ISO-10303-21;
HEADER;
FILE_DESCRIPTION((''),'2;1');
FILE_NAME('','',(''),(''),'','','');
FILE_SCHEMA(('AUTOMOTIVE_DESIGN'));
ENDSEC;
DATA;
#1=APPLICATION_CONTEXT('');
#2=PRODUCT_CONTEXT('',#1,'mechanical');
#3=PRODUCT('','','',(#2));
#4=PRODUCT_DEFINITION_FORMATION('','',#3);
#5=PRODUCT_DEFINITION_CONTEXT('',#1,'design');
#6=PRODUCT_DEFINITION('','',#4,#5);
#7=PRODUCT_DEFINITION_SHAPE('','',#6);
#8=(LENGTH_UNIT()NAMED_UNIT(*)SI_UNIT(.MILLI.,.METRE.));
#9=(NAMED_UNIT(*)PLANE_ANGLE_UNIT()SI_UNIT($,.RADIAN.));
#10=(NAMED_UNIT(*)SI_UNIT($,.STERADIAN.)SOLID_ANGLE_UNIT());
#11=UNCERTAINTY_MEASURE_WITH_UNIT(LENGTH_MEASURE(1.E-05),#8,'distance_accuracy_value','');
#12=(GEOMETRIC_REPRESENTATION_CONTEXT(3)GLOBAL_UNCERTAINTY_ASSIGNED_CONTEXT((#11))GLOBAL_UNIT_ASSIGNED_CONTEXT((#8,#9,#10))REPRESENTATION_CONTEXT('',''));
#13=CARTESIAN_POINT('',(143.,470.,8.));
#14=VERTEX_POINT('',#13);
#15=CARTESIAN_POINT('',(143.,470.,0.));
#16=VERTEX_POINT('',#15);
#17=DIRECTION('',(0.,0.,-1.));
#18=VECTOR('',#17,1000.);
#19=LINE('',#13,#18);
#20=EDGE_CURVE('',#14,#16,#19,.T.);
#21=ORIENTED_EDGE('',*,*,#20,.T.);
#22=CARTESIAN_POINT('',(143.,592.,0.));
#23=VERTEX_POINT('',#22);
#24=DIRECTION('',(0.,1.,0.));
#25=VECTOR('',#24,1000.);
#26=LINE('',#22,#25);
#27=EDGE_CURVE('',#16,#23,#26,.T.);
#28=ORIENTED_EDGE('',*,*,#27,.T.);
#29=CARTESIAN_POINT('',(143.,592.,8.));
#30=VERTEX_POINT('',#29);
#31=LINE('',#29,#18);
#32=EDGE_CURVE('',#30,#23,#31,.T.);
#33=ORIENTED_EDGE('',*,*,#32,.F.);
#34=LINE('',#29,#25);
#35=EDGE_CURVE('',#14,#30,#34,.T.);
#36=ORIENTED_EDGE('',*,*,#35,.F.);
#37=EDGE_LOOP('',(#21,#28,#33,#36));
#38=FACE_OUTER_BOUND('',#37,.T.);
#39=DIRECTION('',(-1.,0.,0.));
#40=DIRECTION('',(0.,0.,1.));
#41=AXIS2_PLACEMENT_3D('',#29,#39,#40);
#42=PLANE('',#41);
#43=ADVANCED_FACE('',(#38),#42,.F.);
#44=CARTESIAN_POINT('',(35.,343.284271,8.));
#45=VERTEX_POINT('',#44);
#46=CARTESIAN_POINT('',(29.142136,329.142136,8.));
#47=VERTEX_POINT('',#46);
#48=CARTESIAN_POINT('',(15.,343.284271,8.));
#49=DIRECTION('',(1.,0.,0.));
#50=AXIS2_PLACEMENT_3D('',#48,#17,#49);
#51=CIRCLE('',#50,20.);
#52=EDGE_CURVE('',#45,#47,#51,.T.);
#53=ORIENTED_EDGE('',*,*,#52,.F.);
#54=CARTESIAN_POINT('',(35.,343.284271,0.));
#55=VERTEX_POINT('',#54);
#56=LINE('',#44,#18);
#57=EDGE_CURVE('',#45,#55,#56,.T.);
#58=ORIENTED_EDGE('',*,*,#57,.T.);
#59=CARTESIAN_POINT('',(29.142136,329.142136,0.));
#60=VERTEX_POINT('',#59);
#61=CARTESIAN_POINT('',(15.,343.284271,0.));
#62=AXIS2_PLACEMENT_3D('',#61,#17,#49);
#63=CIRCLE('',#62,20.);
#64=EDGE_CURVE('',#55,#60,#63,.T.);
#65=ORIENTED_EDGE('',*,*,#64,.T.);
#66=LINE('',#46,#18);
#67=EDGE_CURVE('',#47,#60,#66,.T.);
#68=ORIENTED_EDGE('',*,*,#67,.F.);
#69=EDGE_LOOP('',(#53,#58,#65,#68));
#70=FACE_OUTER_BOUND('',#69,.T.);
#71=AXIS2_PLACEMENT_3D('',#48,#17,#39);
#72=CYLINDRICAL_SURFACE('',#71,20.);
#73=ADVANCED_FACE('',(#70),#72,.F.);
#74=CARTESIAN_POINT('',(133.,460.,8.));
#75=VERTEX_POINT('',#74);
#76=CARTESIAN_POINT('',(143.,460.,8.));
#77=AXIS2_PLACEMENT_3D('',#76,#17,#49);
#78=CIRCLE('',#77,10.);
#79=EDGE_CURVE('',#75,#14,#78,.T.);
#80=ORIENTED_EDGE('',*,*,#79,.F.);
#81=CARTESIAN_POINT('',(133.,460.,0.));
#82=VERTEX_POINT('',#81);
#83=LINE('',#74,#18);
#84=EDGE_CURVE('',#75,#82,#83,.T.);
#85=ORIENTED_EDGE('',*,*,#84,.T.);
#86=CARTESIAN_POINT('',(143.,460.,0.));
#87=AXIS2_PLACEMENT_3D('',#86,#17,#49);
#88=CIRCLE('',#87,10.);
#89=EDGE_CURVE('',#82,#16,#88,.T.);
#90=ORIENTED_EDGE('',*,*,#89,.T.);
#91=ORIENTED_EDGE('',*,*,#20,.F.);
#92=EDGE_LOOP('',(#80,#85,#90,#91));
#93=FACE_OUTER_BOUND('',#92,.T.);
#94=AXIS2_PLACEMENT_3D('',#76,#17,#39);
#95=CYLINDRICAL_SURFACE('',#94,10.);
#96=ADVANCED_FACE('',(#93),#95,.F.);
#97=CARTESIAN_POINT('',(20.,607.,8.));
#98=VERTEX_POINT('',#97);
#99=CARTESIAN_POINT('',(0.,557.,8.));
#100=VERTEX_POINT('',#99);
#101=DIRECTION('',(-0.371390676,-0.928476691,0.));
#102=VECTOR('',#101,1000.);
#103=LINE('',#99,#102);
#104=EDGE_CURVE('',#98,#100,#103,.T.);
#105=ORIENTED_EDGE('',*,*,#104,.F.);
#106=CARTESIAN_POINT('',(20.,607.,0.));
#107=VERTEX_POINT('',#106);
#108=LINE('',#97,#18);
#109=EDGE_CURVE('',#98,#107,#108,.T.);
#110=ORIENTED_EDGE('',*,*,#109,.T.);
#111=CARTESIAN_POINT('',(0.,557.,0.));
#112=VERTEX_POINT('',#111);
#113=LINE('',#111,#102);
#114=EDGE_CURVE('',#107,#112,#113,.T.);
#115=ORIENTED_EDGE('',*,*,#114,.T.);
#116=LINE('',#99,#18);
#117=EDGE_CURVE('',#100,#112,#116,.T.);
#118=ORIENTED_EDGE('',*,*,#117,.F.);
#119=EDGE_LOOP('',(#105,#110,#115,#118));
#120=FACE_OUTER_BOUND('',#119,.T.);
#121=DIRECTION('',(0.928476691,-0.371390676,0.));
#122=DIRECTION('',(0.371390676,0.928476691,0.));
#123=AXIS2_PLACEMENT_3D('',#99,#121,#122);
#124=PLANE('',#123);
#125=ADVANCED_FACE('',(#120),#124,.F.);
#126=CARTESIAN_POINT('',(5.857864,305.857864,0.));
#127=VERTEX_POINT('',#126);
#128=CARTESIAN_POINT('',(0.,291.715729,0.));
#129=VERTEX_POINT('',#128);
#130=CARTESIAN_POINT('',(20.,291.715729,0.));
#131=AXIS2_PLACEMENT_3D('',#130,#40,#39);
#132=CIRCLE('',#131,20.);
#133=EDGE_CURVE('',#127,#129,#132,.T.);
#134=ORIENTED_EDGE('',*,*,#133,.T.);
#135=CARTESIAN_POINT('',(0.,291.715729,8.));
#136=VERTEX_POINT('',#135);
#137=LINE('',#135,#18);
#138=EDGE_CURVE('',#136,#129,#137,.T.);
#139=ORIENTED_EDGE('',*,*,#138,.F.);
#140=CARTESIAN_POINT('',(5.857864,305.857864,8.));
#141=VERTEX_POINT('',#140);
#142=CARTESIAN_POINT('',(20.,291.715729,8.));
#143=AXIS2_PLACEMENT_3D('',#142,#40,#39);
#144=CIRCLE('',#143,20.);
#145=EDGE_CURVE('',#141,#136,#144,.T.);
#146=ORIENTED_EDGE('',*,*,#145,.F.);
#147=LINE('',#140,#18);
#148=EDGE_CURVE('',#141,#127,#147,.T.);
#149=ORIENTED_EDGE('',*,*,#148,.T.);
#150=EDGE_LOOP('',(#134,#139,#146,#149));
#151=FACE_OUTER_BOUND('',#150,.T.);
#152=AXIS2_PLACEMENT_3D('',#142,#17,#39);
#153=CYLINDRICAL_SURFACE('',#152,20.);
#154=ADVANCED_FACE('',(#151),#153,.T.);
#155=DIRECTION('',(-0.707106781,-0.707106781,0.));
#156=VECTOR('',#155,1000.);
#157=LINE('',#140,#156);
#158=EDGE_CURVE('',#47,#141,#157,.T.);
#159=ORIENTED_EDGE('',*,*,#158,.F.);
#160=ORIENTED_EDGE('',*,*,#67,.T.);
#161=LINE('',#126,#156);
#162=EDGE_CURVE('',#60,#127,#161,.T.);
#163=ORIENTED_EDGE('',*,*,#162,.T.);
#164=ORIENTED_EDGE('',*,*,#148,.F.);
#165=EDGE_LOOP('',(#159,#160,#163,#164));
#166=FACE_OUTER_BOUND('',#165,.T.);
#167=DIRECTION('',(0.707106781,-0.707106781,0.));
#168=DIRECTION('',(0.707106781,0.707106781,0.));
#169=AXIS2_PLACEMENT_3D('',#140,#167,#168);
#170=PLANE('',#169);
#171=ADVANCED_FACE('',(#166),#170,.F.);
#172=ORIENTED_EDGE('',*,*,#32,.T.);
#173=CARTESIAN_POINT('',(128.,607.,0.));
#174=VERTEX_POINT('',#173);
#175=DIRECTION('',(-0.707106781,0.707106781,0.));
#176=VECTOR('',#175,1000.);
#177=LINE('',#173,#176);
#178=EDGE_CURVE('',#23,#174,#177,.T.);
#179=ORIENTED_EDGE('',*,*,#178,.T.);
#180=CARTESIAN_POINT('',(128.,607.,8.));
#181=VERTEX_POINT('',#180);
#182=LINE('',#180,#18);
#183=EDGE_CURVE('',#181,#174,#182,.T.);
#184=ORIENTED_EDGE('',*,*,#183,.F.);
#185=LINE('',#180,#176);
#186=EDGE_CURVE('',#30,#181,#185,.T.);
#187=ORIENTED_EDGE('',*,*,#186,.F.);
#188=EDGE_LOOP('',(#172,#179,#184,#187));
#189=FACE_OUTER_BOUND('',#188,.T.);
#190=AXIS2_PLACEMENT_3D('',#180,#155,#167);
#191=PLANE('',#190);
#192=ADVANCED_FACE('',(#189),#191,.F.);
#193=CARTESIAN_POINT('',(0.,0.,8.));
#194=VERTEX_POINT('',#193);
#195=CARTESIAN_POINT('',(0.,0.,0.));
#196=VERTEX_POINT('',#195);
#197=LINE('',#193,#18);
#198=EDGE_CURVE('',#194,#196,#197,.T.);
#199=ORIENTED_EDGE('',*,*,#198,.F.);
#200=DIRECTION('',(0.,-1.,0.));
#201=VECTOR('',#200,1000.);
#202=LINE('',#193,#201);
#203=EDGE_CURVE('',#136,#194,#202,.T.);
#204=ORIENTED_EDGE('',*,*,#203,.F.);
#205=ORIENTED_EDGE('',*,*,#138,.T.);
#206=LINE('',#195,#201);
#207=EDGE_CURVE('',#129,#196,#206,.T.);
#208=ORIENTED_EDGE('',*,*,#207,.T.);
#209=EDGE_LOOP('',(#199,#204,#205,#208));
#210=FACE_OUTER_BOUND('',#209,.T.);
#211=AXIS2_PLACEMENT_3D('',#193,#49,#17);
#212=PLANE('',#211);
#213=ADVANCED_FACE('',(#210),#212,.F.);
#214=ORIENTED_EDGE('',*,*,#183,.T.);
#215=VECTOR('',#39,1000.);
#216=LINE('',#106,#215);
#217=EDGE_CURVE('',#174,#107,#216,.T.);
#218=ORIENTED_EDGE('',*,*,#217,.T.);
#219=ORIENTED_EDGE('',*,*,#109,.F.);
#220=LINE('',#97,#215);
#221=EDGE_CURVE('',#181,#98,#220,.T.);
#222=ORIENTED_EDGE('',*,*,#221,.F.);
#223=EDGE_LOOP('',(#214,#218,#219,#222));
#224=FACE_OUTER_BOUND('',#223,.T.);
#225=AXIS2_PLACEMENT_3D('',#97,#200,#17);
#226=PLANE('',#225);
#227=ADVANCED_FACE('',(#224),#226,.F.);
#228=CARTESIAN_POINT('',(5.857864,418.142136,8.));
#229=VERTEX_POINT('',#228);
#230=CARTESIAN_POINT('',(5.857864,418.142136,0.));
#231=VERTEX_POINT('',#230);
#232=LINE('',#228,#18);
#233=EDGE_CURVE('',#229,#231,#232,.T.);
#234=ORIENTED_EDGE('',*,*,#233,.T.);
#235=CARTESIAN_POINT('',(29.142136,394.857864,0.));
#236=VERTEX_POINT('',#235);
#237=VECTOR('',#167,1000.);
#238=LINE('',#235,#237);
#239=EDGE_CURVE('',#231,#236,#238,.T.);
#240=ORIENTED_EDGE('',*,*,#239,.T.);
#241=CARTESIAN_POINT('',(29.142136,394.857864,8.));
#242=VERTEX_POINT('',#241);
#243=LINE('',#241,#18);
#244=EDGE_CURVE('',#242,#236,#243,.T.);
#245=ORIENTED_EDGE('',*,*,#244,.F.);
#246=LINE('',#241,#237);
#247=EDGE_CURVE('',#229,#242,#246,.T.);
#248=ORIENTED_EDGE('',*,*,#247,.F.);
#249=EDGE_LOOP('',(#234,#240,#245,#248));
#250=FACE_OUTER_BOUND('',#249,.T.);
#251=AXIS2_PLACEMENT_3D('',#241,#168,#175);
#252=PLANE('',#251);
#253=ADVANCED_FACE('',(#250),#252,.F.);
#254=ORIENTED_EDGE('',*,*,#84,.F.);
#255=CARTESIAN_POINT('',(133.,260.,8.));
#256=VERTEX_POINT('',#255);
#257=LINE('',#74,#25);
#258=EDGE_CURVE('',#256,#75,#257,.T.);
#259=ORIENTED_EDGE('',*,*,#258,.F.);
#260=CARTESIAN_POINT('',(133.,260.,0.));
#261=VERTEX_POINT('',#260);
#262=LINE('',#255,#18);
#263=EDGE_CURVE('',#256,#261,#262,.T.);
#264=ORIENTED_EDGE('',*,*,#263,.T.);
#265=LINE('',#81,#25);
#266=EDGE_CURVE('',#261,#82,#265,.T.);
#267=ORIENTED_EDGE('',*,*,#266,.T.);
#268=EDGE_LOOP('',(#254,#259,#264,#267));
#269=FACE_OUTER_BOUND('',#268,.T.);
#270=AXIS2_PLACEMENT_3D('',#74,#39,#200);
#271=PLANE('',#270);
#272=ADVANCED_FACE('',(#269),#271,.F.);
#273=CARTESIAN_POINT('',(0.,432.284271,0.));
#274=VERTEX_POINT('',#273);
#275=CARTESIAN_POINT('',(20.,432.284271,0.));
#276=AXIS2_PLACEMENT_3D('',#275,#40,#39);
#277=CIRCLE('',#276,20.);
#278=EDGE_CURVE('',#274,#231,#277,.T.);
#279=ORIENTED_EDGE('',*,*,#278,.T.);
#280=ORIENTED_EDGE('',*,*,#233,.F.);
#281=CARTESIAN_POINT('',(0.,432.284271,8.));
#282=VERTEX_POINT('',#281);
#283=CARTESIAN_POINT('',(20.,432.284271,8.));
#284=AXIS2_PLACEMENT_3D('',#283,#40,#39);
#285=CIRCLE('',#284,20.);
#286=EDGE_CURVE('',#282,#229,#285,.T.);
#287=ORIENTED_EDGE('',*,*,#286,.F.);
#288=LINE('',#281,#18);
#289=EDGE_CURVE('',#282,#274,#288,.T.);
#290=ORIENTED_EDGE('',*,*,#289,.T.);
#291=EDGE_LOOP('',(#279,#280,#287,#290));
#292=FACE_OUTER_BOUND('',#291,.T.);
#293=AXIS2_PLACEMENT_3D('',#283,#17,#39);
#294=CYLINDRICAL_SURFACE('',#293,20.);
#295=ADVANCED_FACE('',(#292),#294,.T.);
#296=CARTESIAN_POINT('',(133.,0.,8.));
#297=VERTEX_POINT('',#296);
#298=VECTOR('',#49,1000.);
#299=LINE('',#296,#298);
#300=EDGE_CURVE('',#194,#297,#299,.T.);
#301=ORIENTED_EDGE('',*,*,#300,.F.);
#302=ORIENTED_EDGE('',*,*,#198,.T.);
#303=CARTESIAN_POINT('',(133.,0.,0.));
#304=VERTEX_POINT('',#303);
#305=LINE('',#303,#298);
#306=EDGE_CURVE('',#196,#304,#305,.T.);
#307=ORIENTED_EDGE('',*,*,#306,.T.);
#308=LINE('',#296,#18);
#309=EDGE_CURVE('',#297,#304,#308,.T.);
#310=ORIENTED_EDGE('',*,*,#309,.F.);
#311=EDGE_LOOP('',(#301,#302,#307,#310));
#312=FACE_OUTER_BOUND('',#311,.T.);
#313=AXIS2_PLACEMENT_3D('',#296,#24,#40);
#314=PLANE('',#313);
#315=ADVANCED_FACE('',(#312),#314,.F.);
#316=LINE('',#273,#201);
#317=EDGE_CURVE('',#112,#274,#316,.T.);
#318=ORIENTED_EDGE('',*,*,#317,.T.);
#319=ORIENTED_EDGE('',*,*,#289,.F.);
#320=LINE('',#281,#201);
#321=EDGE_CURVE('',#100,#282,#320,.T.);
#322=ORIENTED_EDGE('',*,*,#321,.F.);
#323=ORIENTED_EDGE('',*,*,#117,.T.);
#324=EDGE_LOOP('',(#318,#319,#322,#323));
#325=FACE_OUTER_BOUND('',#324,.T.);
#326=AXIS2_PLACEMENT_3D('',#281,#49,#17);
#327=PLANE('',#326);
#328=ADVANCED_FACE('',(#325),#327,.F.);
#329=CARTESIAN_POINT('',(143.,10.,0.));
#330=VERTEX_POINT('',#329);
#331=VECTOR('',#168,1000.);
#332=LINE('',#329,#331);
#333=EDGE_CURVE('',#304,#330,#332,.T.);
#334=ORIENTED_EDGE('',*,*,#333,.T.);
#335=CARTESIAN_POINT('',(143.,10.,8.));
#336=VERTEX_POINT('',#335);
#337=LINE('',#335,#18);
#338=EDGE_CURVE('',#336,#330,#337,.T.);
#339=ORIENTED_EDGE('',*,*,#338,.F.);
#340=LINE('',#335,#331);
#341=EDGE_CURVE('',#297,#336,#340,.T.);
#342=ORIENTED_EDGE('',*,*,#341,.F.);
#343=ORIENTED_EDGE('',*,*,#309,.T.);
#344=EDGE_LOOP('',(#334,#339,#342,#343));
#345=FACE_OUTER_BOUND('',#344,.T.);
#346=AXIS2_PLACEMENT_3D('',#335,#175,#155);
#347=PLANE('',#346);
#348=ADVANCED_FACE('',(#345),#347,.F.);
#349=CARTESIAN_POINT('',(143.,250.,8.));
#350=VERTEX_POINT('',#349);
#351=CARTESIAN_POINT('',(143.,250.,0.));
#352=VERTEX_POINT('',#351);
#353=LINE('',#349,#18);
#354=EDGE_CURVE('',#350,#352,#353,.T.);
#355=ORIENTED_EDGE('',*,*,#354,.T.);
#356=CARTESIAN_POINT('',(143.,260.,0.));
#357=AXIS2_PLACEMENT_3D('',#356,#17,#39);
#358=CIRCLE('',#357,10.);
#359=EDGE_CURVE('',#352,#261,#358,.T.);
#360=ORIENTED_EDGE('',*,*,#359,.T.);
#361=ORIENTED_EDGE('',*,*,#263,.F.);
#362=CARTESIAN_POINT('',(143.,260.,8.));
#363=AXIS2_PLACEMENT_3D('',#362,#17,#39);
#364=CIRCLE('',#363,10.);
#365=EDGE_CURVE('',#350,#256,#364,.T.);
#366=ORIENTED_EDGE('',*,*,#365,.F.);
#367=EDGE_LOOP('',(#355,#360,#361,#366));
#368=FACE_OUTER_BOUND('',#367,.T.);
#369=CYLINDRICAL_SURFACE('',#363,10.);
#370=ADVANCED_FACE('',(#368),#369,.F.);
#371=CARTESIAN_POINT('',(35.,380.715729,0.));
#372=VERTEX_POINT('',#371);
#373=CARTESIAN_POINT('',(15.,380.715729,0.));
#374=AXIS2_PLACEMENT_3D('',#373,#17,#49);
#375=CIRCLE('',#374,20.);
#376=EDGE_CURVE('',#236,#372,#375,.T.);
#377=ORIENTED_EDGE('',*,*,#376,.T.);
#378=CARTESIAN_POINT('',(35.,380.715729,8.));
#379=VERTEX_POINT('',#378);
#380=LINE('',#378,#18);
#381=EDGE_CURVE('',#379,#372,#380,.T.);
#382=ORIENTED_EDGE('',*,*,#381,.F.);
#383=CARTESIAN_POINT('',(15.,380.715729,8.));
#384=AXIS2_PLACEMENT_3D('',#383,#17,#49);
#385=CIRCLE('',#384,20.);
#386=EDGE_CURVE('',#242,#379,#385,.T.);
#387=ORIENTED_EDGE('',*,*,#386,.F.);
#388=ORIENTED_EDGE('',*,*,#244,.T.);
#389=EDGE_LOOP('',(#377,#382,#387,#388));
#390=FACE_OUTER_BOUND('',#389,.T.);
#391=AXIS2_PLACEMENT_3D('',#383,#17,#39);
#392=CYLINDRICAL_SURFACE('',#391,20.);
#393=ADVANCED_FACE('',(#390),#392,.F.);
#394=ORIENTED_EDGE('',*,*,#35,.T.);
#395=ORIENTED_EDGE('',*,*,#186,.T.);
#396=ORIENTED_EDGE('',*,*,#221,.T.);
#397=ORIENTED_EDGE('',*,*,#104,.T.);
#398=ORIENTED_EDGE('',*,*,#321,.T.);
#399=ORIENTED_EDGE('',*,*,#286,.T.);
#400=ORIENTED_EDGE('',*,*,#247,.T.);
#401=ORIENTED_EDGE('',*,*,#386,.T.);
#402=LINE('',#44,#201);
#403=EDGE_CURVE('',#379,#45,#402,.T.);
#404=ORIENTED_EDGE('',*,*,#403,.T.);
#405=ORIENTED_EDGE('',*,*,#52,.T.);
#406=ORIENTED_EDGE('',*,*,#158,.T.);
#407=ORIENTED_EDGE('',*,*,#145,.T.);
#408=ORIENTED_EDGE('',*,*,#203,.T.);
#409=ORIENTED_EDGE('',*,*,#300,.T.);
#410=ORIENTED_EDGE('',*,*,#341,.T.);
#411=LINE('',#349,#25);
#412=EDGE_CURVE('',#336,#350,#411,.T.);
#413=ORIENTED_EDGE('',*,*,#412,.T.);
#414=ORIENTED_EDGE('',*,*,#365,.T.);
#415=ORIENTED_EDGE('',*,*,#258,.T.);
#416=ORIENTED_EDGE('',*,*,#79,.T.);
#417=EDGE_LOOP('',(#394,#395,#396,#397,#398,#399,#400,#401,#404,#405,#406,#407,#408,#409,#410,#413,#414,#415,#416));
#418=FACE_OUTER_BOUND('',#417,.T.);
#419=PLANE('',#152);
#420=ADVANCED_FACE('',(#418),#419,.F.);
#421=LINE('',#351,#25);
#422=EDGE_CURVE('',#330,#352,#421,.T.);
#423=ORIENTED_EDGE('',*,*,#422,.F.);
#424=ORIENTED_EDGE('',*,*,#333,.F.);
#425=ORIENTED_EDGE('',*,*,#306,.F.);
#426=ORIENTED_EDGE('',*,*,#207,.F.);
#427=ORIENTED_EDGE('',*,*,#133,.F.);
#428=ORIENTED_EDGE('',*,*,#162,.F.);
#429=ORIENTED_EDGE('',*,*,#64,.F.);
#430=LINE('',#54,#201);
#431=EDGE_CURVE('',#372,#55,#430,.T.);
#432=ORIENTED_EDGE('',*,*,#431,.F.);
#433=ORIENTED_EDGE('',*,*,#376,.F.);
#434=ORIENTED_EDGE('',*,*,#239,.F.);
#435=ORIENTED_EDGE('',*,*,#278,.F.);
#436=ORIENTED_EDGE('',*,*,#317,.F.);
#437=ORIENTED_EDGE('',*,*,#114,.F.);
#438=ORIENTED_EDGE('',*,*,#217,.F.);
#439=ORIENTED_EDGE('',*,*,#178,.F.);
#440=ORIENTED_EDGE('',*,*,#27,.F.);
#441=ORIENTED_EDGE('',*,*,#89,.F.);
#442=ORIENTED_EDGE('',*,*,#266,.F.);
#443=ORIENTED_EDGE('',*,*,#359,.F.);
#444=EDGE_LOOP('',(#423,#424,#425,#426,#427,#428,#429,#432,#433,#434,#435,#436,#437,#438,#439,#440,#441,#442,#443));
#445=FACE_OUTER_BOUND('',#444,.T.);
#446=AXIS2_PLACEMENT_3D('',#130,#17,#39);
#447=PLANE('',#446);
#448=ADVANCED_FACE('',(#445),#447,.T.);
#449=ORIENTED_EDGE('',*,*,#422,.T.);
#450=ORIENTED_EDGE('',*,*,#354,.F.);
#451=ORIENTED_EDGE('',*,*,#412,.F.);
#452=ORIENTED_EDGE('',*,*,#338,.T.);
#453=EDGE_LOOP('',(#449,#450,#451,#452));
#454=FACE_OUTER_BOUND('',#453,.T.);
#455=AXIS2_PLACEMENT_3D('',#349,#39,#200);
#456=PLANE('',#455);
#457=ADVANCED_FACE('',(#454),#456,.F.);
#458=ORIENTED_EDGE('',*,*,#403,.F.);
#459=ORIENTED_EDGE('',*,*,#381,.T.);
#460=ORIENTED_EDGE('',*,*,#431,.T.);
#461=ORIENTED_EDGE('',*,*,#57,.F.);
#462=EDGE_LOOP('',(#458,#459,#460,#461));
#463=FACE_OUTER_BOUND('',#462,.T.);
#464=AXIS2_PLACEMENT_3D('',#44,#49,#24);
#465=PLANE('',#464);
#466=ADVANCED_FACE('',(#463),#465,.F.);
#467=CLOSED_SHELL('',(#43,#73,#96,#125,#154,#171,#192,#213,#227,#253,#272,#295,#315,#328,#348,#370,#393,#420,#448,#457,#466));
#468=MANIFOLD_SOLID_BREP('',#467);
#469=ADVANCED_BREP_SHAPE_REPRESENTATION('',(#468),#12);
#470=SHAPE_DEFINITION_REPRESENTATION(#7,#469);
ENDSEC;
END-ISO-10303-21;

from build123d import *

# Parameters (mm, degrees)
BOSS_EXTRUDE1_DEPTH = 8


with BuildPart() as part:
    # Sketch1 → Boss-Extrude1 (new body)
    with BuildSketch(Plane.XY):
        with BuildLine():
            Line((0, 0), (0, 291.715728753))
            ThreePointArc((0, 291.715728753), (1.52240935, 299.3693974), (5.857864376, 305.857864376))
            Line((5.857864376, 305.857864376), (29.142135624, 329.142135624))
            ThreePointArc((29.142135624, 329.142135624), (33.47759065, 335.6306026), (35, 343.284271247))
            Line((35, 343.284271247), (35, 380.715728753))
            ThreePointArc((35, 380.715728753), (33.47759065, 388.3693974), (29.142135624, 394.857864376))
            Line((29.142135624, 394.857864376), (5.857864376, 418.142135624))
            ThreePointArc((5.857864376, 418.142135624), (1.52240935, 424.6306026), (0, 432.284271247))
            Line((0, 432.284271247), (0, 557))
            Line((0, 557), (20, 607))
            Line((20, 607), (128, 607))
            Line((128, 607), (143, 592))
            Line((143, 592), (143, 470))
            ThreePointArc((143, 470), (135.928932188, 467.071067812), (133, 460))
            Line((133, 460), (133, 260))
            ThreePointArc((133, 260), (135.928932188, 252.928932188), (143, 250))
            Line((143, 250), (143, 10))
            Line((143, 10), (133, 0))
            Line((133, 0), (0, 0))
        make_face()
    extrude(amount=BOSS_EXTRUDE1_DEPTH)


solid = part.part
